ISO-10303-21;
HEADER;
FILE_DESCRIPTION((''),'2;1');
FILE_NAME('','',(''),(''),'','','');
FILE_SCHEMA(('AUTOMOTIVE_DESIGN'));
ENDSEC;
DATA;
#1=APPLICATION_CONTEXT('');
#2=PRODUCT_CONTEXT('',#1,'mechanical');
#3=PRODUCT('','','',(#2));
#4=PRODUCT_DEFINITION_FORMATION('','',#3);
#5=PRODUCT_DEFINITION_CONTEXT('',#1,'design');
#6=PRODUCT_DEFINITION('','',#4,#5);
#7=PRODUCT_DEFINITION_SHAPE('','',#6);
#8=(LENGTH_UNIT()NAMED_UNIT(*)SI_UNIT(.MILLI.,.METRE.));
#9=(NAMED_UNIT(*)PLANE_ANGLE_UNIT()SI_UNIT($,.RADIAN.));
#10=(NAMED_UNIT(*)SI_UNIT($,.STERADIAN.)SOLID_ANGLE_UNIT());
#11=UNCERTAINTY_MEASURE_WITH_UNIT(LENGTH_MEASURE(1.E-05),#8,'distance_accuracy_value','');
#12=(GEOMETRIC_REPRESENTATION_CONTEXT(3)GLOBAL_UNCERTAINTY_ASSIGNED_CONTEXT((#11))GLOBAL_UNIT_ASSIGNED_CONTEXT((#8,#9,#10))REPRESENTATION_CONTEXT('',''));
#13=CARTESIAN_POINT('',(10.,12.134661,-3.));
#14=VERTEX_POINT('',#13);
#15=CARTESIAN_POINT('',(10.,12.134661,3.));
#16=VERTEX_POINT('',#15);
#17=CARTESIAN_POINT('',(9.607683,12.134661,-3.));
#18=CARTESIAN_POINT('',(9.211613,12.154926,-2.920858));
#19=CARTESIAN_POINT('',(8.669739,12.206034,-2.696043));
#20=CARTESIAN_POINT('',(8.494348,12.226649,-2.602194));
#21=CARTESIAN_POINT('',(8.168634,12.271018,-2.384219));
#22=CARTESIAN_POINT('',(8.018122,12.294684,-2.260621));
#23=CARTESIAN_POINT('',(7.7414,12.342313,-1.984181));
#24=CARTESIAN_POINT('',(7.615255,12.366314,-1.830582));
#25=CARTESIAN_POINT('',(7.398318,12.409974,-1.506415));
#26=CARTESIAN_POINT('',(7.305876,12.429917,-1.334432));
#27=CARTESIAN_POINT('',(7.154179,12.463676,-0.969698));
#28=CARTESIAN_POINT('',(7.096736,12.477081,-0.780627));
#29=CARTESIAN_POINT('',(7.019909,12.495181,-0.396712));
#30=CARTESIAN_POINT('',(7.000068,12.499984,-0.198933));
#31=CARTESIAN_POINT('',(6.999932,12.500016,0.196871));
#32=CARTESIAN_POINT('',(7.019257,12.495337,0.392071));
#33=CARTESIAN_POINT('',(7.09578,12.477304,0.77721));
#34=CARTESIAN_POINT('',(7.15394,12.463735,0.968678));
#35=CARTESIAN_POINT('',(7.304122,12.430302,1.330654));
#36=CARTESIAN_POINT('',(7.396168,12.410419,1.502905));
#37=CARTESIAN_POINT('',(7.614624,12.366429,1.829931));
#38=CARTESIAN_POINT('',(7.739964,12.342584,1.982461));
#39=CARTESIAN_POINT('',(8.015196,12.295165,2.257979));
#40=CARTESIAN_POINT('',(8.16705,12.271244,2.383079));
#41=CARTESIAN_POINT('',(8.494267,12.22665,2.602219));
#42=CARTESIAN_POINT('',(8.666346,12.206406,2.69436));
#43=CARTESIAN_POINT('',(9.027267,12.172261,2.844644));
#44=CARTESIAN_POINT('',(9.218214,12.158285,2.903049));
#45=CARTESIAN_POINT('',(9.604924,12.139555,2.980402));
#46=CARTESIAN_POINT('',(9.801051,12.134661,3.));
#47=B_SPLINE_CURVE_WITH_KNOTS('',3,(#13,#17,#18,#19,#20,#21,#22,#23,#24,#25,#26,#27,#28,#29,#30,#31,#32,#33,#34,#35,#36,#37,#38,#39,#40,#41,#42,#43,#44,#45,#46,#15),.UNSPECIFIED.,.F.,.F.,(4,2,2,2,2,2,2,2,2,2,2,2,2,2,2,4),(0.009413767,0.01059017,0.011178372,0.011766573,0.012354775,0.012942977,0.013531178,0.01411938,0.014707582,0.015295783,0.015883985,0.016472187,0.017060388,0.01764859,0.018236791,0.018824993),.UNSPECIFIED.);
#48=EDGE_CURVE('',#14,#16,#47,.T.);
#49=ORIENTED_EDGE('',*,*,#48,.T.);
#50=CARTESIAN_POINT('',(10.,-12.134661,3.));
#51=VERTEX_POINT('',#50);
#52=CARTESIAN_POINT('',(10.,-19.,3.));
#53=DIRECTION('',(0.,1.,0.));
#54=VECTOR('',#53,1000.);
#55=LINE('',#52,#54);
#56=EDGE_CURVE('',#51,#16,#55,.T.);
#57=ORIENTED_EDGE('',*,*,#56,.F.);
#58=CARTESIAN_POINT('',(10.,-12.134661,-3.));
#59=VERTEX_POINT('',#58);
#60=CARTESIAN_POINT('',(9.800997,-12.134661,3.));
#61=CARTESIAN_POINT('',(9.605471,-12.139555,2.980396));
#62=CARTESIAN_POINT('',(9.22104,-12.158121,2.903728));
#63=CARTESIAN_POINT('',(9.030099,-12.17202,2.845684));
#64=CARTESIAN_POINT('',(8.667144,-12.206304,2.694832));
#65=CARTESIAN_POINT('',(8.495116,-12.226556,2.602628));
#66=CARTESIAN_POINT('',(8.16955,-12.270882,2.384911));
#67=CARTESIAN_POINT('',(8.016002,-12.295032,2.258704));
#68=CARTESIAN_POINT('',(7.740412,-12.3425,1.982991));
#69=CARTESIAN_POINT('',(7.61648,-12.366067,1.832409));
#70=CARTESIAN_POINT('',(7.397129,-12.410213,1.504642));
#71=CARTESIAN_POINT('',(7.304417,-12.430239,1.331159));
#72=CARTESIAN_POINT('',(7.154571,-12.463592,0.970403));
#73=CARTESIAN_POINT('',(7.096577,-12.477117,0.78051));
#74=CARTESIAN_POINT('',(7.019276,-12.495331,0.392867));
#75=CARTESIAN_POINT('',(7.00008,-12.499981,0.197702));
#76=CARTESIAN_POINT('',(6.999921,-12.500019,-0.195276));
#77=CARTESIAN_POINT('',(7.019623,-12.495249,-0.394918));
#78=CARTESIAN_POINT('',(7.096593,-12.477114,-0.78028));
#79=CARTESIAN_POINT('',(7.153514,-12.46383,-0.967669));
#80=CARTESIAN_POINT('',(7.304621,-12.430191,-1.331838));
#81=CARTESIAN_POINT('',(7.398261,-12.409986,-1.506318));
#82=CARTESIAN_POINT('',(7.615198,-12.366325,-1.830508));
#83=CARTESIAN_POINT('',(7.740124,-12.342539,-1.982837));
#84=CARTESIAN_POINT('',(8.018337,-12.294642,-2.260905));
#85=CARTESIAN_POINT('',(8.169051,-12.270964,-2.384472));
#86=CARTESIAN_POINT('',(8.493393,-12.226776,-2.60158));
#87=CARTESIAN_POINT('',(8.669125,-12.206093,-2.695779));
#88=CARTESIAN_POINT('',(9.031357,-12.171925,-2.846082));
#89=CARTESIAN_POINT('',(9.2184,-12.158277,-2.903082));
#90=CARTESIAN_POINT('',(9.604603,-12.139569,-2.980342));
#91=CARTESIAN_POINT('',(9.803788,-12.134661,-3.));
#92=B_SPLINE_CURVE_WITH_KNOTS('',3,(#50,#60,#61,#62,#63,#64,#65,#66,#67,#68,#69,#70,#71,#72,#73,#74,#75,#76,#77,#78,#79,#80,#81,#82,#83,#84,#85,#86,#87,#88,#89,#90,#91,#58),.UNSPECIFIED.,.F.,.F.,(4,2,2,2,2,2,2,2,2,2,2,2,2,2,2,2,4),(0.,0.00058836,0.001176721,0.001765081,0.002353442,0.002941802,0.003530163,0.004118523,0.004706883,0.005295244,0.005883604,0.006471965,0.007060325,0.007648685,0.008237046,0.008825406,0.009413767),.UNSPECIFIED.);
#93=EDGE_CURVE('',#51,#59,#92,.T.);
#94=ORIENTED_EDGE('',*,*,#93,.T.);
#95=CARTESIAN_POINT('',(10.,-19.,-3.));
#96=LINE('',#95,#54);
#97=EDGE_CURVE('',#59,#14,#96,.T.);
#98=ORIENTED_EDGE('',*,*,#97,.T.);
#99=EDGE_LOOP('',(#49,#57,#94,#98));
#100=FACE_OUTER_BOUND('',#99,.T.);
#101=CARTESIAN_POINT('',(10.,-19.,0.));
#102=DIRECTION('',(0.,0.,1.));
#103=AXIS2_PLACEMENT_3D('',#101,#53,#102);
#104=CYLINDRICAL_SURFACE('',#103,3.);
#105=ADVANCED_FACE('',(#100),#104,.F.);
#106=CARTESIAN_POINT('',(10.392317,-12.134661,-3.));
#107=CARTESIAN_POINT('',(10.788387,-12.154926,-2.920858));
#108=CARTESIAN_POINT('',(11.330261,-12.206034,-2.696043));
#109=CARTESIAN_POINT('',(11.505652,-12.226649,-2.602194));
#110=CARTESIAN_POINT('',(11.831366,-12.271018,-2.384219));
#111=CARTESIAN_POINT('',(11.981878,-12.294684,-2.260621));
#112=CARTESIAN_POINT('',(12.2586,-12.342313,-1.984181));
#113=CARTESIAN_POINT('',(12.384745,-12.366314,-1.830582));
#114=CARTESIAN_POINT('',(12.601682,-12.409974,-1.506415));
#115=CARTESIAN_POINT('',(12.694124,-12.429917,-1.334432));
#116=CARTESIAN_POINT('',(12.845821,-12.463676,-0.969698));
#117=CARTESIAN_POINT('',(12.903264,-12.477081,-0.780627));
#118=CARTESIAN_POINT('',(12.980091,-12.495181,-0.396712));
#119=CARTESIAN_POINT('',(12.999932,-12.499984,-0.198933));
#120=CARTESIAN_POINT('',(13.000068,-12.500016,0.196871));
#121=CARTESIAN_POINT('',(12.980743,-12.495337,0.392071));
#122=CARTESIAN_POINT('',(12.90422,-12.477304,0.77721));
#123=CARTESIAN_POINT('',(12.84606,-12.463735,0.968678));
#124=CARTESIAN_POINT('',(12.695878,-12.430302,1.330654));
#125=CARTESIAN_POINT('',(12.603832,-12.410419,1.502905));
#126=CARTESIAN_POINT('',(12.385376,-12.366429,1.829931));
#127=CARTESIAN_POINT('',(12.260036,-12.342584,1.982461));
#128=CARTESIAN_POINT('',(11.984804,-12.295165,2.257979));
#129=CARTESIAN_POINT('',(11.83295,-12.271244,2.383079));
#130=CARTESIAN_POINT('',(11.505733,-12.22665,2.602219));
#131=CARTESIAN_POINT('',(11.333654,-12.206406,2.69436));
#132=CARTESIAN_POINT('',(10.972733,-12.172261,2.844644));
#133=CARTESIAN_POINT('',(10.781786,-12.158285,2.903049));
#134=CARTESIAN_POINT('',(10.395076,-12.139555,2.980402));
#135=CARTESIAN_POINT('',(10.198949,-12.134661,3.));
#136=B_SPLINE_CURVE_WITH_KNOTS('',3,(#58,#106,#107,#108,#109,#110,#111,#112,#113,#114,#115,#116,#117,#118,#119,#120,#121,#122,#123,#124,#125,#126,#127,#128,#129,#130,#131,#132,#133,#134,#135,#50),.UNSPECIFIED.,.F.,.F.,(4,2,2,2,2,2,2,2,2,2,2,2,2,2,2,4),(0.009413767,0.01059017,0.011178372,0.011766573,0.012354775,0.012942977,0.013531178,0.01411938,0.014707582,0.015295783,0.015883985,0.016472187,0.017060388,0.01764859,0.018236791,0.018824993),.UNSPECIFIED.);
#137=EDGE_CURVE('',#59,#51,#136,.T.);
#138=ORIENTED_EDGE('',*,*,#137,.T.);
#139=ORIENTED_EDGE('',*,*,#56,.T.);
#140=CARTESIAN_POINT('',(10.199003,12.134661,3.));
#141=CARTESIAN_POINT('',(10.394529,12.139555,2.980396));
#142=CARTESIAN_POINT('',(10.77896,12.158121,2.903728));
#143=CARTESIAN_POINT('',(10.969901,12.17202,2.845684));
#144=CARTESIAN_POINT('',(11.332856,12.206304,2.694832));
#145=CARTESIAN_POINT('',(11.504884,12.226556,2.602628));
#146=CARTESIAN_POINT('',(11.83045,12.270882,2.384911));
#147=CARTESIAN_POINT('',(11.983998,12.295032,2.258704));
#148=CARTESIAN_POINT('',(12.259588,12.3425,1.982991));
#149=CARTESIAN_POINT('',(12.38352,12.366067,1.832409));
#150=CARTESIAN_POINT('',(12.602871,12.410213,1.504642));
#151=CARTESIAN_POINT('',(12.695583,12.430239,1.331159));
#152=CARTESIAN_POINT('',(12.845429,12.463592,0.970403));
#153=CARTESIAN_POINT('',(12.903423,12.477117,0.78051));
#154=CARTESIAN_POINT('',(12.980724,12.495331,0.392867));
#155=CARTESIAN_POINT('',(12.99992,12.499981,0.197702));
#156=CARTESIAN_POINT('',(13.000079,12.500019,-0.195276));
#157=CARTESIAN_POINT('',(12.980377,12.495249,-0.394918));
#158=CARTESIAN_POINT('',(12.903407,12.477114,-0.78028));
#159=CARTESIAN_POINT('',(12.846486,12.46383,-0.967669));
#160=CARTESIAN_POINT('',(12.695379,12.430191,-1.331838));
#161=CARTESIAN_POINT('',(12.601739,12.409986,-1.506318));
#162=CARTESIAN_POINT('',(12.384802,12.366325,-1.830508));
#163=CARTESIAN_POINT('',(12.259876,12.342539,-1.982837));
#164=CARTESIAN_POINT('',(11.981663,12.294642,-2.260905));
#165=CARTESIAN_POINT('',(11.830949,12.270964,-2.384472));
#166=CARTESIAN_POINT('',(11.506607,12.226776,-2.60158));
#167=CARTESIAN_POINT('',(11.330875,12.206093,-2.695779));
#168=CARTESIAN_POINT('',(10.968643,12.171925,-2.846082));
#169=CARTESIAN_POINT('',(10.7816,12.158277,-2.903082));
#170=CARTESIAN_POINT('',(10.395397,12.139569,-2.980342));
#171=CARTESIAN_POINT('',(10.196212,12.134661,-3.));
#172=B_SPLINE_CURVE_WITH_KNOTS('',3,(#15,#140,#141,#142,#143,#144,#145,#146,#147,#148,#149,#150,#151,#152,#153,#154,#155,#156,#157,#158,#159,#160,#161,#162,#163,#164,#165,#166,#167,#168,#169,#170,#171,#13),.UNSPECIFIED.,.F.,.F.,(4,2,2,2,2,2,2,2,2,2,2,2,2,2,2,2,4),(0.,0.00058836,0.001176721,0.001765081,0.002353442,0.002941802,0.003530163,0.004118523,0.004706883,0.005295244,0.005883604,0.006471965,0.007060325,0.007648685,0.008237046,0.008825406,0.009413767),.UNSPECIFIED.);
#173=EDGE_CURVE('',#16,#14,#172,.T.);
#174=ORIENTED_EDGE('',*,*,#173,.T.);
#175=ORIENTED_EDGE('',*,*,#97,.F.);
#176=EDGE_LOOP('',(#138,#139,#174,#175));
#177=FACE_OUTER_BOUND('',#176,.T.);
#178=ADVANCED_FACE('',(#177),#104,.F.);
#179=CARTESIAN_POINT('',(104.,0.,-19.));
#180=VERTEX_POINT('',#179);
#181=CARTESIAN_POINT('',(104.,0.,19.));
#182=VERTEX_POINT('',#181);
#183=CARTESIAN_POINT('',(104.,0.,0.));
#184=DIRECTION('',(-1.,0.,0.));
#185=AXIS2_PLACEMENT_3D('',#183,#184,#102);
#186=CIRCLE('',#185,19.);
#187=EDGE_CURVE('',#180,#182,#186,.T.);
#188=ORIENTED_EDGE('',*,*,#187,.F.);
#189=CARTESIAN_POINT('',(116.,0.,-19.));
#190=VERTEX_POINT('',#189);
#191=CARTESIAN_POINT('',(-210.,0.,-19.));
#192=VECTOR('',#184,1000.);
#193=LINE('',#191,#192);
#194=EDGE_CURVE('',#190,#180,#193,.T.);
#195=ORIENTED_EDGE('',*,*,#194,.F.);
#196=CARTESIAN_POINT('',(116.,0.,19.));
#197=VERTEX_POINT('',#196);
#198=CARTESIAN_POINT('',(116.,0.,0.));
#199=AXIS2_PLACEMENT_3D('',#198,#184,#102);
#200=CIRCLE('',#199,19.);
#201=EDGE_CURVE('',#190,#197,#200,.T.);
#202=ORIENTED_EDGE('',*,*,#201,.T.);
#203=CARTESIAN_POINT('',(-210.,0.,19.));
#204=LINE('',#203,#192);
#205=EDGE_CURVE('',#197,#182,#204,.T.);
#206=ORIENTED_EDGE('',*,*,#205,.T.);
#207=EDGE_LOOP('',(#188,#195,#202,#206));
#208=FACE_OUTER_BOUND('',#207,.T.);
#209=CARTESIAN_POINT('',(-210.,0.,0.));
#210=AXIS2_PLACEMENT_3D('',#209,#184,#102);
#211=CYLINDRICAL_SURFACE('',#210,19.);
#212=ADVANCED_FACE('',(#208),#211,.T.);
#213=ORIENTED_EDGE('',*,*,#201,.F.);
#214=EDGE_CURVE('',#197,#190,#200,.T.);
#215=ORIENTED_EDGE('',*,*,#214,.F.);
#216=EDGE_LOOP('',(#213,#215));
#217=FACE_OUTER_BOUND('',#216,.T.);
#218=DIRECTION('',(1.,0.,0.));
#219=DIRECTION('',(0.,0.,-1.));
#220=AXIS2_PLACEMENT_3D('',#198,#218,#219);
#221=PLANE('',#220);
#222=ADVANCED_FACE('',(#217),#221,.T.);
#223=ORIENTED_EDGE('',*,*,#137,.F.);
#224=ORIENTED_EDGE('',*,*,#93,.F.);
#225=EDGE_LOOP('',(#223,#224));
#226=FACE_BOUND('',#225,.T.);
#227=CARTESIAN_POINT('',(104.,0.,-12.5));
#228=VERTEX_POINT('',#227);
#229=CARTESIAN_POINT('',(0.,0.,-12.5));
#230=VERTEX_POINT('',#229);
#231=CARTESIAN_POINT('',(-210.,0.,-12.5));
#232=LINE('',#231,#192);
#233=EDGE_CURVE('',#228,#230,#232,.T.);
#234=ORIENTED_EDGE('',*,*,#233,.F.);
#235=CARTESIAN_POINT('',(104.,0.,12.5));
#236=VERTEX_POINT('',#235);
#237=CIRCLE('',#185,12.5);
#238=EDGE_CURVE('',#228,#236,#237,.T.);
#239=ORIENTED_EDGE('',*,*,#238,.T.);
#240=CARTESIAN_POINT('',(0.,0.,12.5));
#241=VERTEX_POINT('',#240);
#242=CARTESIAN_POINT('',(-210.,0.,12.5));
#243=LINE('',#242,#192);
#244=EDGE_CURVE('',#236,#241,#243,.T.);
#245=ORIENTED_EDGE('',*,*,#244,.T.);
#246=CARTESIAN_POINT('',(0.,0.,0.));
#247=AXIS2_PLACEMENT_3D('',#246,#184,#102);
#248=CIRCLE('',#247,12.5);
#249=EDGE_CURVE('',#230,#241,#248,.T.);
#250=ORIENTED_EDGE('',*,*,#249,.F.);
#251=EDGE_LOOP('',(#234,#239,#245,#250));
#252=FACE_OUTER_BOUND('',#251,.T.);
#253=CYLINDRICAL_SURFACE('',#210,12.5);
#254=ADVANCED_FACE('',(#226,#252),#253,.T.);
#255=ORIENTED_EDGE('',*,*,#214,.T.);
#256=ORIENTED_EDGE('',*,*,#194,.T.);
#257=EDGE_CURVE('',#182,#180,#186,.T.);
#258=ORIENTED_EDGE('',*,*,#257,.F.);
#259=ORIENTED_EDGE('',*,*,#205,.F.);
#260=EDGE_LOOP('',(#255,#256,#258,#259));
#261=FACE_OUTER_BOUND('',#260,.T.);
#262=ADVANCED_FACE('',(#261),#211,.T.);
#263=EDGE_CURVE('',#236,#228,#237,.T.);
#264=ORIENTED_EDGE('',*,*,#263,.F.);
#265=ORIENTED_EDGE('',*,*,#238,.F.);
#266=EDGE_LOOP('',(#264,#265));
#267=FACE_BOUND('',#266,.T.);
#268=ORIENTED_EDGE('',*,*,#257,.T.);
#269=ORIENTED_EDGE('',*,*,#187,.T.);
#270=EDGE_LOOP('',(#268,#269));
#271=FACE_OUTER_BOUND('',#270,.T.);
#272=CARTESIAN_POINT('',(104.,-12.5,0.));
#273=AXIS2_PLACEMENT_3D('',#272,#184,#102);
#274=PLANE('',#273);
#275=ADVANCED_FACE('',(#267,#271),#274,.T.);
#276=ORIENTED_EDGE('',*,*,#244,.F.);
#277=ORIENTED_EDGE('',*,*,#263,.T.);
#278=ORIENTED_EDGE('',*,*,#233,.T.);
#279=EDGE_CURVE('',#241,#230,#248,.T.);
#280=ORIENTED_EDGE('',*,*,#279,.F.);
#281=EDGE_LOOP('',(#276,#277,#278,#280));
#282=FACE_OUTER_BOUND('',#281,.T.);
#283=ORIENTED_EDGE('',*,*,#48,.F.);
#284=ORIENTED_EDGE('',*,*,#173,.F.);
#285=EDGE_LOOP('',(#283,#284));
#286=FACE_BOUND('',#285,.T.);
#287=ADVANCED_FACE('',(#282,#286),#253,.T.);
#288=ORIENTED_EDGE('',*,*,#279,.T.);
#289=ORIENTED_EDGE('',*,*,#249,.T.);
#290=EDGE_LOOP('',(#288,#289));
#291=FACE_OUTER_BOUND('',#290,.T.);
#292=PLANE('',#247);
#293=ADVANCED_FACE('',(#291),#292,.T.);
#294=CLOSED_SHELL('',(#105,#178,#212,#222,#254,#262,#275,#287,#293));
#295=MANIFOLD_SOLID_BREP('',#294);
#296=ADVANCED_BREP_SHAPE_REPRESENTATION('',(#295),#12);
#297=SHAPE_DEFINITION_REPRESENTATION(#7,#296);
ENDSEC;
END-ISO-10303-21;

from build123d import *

# Parameters (mm, degrees)
CROSS_HOLE_6_DEPTH      = 120.071407147
CROSS_HOLE_6_DEPTH_BACK = 120.071407147
CROSS_HOLE_SKETCH_R     = 3


with BuildPart() as part:
    # Pin Profile Sketch → Headed Pin Body (revolve)
    with BuildSketch(Plane.XY, mode=Mode.PRIVATE) as headed_pin_body_sk:
        Polygon((0, 0), (84, 0), (116, 0), (116, -19), (104, -19), (104, -12.5), (0, -12.5), align=None)
    revolve(headed_pin_body_sk.sketch.rotate(Axis((-210, 0, 0), (1, 0, 0)), 270), axis=Axis((-210, 0, 0), (1, 0, 0)))

    # Cross Hole Sketch → Cross Hole Ø6 (cut, two sides: drawn at the far end of the back side and taken through both)
    with BuildSketch(Plane(origin=(0, 0, 0), x_dir=(1, 0, 0), z_dir=(0, 1, 0)).offset(-CROSS_HOLE_6_DEPTH_BACK)):
        with Locations(Location((10, 0, 0), (0, 0, 270))):
            Circle(CROSS_HOLE_SKETCH_R)
    extrude(amount=CROSS_HOLE_6_DEPTH + CROSS_HOLE_6_DEPTH_BACK, mode=Mode.SUBTRACT)


solid = part.part
